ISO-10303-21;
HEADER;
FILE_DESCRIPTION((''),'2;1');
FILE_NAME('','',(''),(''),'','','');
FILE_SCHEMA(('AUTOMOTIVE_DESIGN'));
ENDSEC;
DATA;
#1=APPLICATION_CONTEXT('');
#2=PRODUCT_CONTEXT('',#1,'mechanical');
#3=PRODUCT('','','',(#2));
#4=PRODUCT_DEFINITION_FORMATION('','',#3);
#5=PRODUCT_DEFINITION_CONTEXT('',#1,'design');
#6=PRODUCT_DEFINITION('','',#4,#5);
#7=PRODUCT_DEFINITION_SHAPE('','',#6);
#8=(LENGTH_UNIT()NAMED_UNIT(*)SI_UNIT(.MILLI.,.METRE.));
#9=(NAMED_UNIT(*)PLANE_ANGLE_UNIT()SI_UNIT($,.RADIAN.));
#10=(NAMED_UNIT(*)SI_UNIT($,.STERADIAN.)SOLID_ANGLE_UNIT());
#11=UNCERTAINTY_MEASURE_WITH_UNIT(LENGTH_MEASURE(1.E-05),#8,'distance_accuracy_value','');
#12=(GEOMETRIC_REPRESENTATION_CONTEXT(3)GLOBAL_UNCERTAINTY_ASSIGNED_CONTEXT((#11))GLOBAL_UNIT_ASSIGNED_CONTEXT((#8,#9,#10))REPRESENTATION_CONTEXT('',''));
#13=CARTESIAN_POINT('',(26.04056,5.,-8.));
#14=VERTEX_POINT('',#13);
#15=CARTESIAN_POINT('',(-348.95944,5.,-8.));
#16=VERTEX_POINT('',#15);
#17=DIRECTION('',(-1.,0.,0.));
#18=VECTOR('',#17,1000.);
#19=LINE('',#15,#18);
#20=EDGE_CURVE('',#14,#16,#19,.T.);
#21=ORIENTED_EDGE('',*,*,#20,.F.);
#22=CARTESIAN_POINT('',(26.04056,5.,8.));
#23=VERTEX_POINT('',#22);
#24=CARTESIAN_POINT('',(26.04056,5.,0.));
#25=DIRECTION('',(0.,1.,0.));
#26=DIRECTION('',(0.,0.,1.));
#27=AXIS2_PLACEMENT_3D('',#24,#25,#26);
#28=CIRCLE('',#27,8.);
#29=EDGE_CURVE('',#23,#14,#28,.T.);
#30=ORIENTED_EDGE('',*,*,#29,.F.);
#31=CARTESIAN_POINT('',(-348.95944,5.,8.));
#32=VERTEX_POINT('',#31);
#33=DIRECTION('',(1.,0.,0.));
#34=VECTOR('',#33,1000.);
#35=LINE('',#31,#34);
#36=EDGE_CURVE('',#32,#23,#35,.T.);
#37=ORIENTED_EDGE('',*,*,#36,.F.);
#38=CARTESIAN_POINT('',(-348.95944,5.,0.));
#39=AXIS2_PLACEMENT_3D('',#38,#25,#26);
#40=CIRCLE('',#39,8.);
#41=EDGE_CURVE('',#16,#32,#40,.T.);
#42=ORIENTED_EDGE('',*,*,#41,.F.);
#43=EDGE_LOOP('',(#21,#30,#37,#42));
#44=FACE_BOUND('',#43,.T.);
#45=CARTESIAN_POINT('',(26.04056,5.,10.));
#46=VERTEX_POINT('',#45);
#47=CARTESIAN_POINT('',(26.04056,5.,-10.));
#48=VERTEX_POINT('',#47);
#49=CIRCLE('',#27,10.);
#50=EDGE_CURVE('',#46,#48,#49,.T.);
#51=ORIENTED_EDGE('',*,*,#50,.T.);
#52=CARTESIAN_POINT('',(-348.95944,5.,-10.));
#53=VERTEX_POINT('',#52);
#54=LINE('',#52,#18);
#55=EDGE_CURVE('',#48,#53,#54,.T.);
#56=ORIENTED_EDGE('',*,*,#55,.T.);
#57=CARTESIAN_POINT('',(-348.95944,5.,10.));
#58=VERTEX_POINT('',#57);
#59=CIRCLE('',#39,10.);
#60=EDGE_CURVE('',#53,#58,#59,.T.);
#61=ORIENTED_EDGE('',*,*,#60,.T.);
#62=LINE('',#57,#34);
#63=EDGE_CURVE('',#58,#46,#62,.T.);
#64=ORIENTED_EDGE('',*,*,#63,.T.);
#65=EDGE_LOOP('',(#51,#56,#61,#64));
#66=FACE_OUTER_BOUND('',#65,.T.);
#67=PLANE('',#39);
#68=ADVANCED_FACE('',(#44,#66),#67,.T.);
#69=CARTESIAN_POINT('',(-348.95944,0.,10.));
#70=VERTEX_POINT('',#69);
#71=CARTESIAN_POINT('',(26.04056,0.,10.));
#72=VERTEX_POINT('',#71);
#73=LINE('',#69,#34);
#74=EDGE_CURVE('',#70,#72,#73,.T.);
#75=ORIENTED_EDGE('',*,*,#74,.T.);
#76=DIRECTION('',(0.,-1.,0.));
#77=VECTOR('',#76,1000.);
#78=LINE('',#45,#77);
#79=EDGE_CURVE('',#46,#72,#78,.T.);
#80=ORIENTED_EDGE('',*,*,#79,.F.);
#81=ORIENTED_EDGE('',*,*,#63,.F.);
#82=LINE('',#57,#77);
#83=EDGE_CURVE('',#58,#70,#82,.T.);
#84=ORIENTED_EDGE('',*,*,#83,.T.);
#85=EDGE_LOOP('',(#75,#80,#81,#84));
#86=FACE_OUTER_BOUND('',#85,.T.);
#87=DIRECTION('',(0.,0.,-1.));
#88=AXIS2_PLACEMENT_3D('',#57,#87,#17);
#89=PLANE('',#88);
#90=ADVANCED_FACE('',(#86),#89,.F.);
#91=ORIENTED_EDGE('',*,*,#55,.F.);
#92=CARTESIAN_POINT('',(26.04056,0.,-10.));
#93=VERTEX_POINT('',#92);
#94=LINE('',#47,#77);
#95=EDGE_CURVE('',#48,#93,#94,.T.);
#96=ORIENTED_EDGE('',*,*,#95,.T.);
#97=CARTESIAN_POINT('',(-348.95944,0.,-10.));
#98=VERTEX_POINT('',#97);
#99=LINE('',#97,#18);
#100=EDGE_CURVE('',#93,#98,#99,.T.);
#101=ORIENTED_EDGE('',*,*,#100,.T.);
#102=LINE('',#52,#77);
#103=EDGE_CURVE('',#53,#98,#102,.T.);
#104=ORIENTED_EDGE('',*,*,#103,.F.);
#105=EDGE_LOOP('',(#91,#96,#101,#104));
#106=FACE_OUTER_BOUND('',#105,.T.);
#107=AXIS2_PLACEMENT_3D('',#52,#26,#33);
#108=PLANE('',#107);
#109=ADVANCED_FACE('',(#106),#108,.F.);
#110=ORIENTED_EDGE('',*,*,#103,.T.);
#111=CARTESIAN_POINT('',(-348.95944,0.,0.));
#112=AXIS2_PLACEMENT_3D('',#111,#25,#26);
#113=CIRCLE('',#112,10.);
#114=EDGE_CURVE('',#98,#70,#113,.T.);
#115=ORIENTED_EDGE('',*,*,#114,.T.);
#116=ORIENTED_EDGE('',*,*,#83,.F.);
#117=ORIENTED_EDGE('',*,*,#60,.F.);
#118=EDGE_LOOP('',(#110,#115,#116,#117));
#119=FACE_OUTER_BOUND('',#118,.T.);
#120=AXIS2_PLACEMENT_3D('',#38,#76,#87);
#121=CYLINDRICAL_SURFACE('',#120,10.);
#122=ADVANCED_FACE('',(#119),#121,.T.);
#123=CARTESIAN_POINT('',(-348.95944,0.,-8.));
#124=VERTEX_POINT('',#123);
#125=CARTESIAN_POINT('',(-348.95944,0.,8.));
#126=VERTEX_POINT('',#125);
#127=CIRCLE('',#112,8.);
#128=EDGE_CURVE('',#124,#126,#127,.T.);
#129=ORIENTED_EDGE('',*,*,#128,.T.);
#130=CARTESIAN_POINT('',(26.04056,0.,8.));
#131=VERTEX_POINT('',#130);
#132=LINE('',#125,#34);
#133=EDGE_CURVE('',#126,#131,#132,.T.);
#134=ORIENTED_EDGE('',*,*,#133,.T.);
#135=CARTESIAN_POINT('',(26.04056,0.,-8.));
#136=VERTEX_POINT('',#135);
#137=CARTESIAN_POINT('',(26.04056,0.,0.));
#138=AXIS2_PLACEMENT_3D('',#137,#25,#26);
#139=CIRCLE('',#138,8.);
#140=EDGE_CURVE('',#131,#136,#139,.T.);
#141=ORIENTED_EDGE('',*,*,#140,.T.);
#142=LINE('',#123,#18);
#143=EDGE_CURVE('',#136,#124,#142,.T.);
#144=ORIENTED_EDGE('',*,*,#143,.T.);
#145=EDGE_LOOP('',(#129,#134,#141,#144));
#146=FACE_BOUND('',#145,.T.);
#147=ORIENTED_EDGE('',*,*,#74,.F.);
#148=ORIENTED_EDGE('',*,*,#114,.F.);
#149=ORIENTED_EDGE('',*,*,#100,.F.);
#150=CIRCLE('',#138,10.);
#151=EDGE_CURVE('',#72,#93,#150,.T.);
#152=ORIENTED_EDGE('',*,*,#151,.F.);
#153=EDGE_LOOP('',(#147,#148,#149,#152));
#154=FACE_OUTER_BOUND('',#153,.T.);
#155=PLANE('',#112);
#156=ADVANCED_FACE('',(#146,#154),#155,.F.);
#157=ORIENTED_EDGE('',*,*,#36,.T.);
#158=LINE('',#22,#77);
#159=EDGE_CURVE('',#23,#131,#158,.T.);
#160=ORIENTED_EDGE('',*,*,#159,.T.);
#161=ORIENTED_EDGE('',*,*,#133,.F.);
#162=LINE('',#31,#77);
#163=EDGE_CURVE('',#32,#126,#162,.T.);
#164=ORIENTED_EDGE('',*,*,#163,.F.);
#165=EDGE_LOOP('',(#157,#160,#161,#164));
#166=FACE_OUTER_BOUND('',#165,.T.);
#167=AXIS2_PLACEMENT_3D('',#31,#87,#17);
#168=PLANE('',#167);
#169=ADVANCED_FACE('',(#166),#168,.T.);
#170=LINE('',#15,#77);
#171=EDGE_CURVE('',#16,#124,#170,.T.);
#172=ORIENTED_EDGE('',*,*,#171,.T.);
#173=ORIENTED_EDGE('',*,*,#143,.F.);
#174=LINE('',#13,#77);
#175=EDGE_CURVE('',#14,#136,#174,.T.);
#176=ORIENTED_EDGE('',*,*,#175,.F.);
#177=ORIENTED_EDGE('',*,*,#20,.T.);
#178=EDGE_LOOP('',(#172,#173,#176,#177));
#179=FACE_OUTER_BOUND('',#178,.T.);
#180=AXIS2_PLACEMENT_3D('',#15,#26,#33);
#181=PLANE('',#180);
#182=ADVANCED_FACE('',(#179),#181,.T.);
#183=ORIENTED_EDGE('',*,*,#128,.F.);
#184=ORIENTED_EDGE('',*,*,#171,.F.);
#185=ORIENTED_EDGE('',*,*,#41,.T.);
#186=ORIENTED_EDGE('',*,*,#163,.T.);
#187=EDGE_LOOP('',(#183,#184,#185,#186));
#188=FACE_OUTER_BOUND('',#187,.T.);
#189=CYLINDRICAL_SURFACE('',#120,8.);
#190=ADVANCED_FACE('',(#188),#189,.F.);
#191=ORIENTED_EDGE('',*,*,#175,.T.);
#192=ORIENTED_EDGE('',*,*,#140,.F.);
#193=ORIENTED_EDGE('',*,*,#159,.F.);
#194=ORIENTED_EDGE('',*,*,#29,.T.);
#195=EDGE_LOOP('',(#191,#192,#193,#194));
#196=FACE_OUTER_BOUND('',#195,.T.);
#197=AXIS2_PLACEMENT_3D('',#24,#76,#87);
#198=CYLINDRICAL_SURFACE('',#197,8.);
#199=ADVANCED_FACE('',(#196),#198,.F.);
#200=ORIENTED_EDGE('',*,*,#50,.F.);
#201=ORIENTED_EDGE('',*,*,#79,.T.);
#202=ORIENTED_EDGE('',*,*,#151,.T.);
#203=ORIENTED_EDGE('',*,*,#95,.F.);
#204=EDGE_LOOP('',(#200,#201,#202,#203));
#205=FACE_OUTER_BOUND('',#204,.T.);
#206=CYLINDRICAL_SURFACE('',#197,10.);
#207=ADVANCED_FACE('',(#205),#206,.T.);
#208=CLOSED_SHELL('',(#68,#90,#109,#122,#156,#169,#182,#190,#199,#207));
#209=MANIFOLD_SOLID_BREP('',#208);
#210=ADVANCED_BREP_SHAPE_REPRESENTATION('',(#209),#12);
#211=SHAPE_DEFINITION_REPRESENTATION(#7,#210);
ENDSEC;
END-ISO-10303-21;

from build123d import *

# Parameters (mm, degrees)
BOSS_EXTRUDE1_DEPTH = 5


with BuildPart() as part:
    # Sketch1 → Boss-Extrude1 (new body)
    with BuildSketch(Plane(origin=(0, 0, 0), x_dir=(1, 0, 0), z_dir=(0, 1, 0))):
        with BuildLine():
            Line((-348.959440129, 10), (26.040559871, 10))
            ThreePointArc((26.040559871, 10), (36.040559871, 0), (26.040559871, -10))
            Line((26.040559871, -10), (-348.959440129, -10))
            ThreePointArc((-348.959440129, -10), (-358.959440129, 0), (-348.959440129, 10))
        make_face()
        with BuildLine():
            Line((-348.959440129, 8), (26.040559871, 8))
            ThreePointArc((26.040559871, 8), (34.040559871, 0), (26.040559871, -8))
            Line((26.040559871, -8), (-348.959440129, -8))
            ThreePointArc((-348.959440129, -8), (-356.959440129, 0), (-348.959440129, 8))
        make_face(mode=Mode.SUBTRACT)
    extrude(amount=BOSS_EXTRUDE1_DEPTH)


solid = part.part
